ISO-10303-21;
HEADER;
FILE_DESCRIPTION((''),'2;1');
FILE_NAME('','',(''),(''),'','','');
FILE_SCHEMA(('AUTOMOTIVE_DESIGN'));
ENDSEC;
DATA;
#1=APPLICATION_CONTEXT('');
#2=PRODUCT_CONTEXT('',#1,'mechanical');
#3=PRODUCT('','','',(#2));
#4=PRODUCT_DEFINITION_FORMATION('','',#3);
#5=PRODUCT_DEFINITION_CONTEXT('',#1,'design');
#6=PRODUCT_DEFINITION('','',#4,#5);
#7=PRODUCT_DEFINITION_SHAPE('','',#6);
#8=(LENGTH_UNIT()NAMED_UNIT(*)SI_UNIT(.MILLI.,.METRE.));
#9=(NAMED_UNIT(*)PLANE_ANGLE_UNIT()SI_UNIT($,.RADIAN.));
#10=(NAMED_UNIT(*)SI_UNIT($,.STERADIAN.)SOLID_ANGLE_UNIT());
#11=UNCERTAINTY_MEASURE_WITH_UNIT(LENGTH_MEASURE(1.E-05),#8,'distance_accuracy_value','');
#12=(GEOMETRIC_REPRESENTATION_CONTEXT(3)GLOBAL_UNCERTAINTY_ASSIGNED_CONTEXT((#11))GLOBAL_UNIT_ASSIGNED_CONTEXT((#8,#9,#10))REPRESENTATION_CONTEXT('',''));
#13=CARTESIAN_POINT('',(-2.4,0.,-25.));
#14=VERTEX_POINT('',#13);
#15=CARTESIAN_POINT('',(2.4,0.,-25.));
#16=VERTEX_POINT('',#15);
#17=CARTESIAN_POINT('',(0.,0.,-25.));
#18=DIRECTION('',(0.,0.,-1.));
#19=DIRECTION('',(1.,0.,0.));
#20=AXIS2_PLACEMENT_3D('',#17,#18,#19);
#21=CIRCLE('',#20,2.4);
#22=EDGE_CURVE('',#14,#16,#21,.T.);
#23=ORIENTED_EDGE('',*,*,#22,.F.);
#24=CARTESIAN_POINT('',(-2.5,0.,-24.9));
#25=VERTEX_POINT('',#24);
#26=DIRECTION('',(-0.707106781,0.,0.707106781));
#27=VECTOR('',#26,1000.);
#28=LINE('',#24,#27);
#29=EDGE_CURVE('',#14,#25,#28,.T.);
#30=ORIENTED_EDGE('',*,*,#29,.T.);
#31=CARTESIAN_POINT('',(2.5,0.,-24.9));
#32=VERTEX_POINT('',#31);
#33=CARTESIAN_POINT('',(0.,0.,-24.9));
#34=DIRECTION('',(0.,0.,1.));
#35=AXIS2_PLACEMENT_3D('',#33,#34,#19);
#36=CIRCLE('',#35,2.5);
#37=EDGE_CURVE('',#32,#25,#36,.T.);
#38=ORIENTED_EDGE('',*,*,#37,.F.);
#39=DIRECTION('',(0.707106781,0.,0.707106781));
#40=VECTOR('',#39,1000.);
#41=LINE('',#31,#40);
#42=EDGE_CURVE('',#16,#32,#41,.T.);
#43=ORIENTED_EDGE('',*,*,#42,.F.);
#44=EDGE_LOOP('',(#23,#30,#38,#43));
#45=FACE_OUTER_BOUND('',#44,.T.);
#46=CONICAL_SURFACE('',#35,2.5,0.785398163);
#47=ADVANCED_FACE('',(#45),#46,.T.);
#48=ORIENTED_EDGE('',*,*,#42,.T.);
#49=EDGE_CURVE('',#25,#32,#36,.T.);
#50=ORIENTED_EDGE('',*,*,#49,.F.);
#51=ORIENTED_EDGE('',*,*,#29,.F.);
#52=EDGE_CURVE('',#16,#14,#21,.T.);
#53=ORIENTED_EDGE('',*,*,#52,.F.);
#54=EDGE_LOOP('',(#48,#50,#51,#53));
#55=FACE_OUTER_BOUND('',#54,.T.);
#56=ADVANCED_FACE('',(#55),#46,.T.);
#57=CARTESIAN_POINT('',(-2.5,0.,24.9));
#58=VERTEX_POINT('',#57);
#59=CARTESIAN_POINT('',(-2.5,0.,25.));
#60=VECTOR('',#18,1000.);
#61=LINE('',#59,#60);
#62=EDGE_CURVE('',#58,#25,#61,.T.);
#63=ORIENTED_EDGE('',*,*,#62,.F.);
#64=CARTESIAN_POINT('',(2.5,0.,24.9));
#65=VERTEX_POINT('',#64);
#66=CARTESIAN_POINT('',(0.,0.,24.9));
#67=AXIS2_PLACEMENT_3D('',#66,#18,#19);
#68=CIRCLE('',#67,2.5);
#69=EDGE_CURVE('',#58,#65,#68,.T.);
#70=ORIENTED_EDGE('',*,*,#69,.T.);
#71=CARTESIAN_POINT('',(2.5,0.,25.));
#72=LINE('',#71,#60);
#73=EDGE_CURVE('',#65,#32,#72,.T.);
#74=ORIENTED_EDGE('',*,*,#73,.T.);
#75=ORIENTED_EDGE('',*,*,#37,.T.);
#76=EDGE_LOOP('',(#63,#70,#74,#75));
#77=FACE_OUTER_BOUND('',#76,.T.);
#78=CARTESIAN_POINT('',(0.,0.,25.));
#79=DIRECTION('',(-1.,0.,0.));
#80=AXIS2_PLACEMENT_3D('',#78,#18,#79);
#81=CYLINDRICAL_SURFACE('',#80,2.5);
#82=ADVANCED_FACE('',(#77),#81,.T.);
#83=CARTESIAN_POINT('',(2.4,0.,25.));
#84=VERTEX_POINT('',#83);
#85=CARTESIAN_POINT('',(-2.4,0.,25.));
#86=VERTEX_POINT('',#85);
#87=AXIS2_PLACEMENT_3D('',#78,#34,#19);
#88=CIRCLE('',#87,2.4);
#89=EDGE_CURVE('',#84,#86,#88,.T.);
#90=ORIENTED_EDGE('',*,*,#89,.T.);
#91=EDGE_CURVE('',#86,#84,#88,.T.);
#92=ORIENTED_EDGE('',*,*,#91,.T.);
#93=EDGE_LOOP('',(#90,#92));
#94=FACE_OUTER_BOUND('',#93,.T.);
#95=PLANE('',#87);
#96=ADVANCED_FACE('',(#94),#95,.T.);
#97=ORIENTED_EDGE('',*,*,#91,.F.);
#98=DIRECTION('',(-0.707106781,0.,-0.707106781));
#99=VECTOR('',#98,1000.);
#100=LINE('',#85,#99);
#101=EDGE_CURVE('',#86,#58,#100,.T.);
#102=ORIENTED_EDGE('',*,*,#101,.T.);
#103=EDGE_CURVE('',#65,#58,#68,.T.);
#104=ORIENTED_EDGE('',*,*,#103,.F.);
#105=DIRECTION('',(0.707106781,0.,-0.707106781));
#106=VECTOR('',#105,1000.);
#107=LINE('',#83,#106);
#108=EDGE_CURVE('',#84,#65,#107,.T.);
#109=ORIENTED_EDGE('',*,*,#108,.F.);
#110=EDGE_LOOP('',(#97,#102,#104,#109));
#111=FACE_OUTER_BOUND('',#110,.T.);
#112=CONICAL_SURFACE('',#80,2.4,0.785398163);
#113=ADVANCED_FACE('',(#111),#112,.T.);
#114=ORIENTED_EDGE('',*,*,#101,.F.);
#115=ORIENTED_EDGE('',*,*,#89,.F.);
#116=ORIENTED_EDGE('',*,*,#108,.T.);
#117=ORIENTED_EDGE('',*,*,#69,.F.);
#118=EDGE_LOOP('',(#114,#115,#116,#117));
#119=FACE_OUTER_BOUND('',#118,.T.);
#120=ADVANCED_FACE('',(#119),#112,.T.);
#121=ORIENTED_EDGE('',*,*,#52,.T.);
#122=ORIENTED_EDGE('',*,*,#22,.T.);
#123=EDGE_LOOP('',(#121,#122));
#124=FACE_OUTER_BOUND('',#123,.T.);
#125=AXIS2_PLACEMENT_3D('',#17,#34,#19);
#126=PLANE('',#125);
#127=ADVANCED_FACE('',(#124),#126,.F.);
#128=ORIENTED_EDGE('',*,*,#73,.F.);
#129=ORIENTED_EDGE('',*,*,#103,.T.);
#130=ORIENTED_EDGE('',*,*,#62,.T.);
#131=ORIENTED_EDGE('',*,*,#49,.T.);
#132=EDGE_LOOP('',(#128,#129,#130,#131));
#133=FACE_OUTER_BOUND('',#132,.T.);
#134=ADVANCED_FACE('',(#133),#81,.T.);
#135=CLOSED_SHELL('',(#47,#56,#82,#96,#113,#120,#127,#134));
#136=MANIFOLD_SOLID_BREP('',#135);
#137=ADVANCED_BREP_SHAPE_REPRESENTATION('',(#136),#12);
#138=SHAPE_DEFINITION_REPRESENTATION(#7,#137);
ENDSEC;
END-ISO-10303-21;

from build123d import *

# Parameters (mm, degrees)
SKETCH1_R           = 2.5
BOSS_EXTRUDE1_DEPTH = 25
CHAMFER1_SIZE       = 0.1


with BuildPart() as part:
    # Sketch1 → Boss-Extrude1 (new, symmetric)
    with BuildSketch(Plane.XY):
        Circle(SKETCH1_R)
    extrude(amount=BOSS_EXTRUDE1_DEPTH, both=True)

    # Chamfer1
    chamfer1_edges = [part.edges().sort_by_distance(p)[0] for p in [
        (-2.5, 0, -25),
        (-2.5, 0, 25),
    ]]
    chamfer(chamfer1_edges, length=CHAMFER1_SIZE)


solid = part.part
